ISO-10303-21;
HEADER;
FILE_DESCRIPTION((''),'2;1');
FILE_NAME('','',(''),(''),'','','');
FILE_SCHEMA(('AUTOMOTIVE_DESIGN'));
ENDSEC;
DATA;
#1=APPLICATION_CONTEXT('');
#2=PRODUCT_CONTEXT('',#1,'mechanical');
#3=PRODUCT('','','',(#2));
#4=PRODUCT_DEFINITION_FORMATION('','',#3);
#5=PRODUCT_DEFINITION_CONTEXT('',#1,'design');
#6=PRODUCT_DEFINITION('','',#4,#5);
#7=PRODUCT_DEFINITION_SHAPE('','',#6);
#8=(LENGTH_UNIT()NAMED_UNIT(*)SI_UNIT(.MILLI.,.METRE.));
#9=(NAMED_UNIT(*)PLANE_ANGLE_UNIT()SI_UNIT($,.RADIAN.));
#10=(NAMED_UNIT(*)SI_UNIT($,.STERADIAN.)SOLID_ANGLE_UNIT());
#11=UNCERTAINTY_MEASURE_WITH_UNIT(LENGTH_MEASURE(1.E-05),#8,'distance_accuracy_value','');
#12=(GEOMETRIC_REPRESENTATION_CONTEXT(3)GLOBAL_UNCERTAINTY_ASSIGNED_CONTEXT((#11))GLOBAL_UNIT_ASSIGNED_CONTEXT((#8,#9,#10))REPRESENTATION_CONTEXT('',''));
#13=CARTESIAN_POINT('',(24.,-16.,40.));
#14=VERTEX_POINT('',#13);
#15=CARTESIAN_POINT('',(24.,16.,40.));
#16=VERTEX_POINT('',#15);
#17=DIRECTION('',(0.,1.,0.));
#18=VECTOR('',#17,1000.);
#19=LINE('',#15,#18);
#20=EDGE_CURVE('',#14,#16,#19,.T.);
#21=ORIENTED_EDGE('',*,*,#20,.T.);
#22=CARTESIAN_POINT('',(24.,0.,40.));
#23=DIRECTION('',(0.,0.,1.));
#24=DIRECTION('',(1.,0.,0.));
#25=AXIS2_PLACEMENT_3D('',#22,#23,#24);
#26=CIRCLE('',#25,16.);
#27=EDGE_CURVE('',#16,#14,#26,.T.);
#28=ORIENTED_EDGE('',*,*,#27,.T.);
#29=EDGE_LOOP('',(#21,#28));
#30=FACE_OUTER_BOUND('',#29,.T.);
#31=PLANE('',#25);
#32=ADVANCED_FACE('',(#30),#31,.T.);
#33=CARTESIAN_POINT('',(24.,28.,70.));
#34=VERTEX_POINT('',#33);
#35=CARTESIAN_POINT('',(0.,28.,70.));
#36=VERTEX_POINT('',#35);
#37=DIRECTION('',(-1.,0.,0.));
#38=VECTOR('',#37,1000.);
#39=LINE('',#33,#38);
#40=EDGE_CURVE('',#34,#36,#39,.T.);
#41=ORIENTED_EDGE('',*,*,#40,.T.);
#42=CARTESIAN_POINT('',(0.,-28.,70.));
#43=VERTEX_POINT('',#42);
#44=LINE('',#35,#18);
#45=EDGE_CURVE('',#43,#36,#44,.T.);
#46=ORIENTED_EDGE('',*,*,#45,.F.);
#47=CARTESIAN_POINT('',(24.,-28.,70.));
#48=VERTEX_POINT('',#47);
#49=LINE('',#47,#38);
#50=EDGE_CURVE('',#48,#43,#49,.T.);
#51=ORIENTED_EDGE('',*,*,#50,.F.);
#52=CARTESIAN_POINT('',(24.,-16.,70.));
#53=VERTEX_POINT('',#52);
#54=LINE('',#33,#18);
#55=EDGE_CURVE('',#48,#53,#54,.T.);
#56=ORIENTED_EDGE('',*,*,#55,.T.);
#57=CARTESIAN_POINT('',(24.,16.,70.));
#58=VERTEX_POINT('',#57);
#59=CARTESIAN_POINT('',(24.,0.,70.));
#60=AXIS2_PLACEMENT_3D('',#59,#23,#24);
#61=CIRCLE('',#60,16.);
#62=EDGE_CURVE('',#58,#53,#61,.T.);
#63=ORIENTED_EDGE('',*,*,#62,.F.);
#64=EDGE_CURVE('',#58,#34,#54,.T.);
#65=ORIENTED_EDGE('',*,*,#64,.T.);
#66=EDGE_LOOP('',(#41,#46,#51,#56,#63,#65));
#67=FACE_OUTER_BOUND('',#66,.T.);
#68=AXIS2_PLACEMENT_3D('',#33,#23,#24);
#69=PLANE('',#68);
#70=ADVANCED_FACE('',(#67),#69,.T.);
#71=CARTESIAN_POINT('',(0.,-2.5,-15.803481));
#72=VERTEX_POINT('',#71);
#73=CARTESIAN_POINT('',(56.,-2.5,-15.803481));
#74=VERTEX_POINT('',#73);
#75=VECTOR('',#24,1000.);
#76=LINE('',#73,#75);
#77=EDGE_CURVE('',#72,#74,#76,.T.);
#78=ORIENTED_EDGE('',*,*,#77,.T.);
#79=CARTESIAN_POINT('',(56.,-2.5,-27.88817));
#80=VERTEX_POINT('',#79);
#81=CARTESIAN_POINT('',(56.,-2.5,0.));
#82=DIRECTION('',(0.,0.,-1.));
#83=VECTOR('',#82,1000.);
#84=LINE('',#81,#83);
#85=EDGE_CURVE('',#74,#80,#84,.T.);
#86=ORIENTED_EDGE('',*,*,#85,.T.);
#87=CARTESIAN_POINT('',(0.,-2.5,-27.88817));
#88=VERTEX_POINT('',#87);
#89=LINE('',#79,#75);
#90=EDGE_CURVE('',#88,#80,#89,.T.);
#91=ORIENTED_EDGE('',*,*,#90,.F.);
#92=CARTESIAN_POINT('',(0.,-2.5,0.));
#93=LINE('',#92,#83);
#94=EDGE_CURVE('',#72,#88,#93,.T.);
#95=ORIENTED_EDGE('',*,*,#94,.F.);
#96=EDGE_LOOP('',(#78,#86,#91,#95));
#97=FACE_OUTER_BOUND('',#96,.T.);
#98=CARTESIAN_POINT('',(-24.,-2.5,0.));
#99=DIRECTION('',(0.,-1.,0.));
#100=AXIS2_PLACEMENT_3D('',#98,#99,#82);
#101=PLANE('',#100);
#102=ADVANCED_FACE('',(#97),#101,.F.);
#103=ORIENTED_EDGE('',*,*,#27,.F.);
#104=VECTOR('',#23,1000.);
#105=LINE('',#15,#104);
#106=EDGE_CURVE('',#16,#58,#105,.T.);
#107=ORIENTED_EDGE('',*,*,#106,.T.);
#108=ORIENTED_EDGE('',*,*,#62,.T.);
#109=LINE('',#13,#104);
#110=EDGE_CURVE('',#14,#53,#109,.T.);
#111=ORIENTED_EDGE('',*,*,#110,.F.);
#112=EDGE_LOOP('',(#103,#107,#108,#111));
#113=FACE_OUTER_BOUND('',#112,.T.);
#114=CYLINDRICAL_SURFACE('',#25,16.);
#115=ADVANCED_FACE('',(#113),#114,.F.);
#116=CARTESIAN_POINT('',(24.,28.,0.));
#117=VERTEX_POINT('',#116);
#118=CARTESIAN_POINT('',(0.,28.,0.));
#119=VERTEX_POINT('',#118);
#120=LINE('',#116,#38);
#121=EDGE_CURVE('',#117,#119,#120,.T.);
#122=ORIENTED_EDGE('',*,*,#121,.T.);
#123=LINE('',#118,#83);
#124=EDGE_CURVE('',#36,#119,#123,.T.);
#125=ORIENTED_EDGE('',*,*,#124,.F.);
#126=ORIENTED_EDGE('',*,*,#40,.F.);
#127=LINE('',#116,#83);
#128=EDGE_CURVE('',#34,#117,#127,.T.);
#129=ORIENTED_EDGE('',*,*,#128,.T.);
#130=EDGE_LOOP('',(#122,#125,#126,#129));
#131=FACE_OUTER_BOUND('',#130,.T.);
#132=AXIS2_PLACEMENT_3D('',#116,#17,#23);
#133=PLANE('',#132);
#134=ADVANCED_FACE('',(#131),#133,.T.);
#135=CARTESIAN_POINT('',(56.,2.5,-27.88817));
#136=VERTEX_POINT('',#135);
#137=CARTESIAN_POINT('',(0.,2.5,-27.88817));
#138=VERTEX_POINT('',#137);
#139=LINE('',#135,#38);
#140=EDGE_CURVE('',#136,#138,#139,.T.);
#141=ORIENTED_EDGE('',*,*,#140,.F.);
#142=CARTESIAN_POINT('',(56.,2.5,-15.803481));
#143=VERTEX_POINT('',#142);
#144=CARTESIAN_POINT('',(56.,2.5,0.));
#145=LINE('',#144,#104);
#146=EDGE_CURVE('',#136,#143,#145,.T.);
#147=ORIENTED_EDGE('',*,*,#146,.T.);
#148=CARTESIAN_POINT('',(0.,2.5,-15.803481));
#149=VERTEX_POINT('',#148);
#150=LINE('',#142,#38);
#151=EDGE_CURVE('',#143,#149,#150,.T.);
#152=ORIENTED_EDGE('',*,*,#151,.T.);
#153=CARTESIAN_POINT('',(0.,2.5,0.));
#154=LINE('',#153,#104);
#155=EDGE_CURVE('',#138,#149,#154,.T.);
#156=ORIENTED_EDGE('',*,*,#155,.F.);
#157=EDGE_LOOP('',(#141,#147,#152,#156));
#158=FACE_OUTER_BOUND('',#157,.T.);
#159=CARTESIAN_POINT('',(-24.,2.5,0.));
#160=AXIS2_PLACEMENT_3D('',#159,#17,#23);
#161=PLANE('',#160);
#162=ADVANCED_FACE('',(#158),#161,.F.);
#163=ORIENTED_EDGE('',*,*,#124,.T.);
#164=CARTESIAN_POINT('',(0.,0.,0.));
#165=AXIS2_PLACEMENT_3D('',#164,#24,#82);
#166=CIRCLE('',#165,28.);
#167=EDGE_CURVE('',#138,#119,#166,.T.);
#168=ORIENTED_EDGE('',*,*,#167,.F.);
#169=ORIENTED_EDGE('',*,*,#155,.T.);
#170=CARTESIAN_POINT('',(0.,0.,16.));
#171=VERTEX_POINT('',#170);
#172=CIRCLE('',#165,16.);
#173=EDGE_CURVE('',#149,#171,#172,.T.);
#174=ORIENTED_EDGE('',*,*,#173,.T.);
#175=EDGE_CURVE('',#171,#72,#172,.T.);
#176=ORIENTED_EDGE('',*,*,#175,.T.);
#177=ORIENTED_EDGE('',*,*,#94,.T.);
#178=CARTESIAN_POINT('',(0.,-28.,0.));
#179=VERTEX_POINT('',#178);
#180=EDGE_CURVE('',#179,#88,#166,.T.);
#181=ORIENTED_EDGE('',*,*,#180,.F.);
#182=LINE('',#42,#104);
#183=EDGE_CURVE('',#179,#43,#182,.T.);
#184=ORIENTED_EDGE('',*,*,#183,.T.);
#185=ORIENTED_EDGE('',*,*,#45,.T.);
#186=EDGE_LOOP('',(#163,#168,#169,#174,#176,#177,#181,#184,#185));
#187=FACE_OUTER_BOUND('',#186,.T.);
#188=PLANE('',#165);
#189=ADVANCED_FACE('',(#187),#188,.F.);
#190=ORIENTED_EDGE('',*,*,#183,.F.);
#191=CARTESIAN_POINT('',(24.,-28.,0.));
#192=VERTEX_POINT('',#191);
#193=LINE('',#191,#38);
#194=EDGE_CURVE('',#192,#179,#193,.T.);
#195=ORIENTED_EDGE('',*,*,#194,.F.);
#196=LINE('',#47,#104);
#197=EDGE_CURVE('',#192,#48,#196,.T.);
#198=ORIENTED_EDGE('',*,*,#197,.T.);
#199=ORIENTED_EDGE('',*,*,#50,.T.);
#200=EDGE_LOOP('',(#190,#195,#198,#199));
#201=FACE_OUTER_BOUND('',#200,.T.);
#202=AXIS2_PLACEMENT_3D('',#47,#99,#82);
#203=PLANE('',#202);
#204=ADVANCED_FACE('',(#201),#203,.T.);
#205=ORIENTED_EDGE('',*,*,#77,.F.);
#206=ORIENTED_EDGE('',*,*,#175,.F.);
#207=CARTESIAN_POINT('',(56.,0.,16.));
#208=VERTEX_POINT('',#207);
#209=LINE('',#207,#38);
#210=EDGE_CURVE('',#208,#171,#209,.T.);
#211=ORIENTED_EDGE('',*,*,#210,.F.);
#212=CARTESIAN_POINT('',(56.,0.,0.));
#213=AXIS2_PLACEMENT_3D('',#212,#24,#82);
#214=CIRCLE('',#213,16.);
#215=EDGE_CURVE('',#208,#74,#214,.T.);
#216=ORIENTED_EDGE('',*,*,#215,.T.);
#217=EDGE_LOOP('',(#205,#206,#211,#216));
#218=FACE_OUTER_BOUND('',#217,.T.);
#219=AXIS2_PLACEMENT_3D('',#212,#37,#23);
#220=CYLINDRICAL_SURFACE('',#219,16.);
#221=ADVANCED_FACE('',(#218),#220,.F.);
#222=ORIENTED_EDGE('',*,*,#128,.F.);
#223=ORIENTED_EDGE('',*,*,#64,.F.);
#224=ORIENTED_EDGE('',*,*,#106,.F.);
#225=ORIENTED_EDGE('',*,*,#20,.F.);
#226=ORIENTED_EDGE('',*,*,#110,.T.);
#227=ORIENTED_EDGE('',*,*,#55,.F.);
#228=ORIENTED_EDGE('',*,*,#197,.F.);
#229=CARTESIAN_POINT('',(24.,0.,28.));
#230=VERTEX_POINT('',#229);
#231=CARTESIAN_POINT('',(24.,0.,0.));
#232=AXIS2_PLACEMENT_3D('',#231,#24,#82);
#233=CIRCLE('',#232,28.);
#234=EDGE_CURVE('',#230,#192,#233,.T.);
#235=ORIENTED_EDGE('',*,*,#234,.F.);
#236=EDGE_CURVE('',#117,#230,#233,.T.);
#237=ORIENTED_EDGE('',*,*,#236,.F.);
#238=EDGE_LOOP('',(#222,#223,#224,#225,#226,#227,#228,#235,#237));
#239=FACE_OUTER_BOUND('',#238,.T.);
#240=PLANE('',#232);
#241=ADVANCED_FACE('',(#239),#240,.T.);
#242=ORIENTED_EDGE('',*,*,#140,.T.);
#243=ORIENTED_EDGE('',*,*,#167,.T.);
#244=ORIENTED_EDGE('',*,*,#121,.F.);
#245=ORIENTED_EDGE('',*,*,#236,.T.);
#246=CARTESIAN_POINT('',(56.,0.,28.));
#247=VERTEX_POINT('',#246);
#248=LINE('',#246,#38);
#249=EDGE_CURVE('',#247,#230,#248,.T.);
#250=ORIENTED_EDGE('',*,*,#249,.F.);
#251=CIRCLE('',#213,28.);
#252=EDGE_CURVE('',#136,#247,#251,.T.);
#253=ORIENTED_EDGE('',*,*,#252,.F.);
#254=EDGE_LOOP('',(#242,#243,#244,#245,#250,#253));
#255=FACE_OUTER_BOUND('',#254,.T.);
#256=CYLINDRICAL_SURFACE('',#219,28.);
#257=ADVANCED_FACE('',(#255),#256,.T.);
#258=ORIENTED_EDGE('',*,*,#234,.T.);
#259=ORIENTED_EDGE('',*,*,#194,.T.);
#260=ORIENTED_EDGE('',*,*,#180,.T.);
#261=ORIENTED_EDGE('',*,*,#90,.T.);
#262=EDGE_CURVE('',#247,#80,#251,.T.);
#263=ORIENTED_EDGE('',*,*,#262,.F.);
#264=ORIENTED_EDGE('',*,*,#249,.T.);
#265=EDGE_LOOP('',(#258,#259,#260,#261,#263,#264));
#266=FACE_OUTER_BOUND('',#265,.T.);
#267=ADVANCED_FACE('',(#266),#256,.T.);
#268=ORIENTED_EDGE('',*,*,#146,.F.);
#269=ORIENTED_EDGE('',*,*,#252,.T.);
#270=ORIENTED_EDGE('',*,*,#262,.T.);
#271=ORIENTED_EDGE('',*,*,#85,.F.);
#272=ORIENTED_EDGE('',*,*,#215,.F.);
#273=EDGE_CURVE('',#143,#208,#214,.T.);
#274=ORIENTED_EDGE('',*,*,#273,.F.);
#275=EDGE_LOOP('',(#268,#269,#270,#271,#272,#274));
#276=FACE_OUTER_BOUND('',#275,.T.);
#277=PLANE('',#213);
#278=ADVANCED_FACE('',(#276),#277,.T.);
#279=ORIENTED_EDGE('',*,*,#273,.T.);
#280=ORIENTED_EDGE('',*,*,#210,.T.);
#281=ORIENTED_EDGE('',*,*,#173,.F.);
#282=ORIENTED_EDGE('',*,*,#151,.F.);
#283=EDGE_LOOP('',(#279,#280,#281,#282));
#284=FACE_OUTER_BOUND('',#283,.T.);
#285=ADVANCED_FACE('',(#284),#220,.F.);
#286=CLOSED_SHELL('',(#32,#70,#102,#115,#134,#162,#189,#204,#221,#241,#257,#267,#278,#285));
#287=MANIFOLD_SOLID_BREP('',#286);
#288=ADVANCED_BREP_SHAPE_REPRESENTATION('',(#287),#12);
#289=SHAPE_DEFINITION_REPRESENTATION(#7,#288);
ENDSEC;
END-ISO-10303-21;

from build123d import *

# Parameters (mm, degrees)
BASE_BLOCK_SKETCH_R   = 28
BASE_BLOCK_SKETCH_R_2 = 16
BASE_BLOCK_DEPTH      = 56
CLAMP_BOSS_DEPTH      = 24
SIDE_WINDOW_CUT_DEPTH = 54
BORE_DEPTH            = 30
CLAMP_SLIT_2_5_DEPTH  = 80


with BuildPart() as part:
    # Base Block Sketch → Base Block (new body)
    with BuildSketch(Plane(origin=(0, 0, 0), x_dir=(0, 0, -1), z_dir=(1, 0, 0))):
        Circle(BASE_BLOCK_SKETCH_R)
        Circle(BASE_BLOCK_SKETCH_R_2, mode=Mode.SUBTRACT)
    extrude(amount=BASE_BLOCK_DEPTH)

    # Clamp Boss Sketch → Clamp Boss (add)
    with BuildSketch(Plane.ZY):
        Polygon((0, 0), (0, 28), (70, 28), (70, -28), (0, -28), align=None)
    extrude(amount=-CLAMP_BOSS_DEPTH)

    # Side Window Sketch → Side Window Cut (cut)
    with BuildSketch(Plane.ZY):
        with BuildLine():
            Line((0, 16), (0, -16))
            ThreePointArc((0, -16), (16, 0), (0, 16))
        make_face()
    extrude(amount=-SIDE_WINDOW_CUT_DEPTH, mode=Mode.SUBTRACT)

    # Bore Sketch → Bore (cut)
    with BuildSketch(Plane.XY.offset(70)):
        with BuildLine():
            Line((24, 16), (24, -16))
            ThreePointArc((24, -16), (8, 0), (24, 16))
        make_face()
    extrude(amount=-BORE_DEPTH, mode=Mode.SUBTRACT)

    # Clamp Slit Sketch → Clamp Slit 2.5 (cut)
    with BuildSketch(Plane(origin=(56, 0, 0), x_dir=(0, 0, -1), z_dir=(1, 0, 0))):
        Polygon((30.140731053, 0), (30.140731053, 2.5), (15.803480629, 2.5), (15.803480629, -2.5), (30.140731053, -2.5), align=None)
    extrude(amount=-CLAMP_SLIT_2_5_DEPTH, mode=Mode.SUBTRACT)


solid = part.part
